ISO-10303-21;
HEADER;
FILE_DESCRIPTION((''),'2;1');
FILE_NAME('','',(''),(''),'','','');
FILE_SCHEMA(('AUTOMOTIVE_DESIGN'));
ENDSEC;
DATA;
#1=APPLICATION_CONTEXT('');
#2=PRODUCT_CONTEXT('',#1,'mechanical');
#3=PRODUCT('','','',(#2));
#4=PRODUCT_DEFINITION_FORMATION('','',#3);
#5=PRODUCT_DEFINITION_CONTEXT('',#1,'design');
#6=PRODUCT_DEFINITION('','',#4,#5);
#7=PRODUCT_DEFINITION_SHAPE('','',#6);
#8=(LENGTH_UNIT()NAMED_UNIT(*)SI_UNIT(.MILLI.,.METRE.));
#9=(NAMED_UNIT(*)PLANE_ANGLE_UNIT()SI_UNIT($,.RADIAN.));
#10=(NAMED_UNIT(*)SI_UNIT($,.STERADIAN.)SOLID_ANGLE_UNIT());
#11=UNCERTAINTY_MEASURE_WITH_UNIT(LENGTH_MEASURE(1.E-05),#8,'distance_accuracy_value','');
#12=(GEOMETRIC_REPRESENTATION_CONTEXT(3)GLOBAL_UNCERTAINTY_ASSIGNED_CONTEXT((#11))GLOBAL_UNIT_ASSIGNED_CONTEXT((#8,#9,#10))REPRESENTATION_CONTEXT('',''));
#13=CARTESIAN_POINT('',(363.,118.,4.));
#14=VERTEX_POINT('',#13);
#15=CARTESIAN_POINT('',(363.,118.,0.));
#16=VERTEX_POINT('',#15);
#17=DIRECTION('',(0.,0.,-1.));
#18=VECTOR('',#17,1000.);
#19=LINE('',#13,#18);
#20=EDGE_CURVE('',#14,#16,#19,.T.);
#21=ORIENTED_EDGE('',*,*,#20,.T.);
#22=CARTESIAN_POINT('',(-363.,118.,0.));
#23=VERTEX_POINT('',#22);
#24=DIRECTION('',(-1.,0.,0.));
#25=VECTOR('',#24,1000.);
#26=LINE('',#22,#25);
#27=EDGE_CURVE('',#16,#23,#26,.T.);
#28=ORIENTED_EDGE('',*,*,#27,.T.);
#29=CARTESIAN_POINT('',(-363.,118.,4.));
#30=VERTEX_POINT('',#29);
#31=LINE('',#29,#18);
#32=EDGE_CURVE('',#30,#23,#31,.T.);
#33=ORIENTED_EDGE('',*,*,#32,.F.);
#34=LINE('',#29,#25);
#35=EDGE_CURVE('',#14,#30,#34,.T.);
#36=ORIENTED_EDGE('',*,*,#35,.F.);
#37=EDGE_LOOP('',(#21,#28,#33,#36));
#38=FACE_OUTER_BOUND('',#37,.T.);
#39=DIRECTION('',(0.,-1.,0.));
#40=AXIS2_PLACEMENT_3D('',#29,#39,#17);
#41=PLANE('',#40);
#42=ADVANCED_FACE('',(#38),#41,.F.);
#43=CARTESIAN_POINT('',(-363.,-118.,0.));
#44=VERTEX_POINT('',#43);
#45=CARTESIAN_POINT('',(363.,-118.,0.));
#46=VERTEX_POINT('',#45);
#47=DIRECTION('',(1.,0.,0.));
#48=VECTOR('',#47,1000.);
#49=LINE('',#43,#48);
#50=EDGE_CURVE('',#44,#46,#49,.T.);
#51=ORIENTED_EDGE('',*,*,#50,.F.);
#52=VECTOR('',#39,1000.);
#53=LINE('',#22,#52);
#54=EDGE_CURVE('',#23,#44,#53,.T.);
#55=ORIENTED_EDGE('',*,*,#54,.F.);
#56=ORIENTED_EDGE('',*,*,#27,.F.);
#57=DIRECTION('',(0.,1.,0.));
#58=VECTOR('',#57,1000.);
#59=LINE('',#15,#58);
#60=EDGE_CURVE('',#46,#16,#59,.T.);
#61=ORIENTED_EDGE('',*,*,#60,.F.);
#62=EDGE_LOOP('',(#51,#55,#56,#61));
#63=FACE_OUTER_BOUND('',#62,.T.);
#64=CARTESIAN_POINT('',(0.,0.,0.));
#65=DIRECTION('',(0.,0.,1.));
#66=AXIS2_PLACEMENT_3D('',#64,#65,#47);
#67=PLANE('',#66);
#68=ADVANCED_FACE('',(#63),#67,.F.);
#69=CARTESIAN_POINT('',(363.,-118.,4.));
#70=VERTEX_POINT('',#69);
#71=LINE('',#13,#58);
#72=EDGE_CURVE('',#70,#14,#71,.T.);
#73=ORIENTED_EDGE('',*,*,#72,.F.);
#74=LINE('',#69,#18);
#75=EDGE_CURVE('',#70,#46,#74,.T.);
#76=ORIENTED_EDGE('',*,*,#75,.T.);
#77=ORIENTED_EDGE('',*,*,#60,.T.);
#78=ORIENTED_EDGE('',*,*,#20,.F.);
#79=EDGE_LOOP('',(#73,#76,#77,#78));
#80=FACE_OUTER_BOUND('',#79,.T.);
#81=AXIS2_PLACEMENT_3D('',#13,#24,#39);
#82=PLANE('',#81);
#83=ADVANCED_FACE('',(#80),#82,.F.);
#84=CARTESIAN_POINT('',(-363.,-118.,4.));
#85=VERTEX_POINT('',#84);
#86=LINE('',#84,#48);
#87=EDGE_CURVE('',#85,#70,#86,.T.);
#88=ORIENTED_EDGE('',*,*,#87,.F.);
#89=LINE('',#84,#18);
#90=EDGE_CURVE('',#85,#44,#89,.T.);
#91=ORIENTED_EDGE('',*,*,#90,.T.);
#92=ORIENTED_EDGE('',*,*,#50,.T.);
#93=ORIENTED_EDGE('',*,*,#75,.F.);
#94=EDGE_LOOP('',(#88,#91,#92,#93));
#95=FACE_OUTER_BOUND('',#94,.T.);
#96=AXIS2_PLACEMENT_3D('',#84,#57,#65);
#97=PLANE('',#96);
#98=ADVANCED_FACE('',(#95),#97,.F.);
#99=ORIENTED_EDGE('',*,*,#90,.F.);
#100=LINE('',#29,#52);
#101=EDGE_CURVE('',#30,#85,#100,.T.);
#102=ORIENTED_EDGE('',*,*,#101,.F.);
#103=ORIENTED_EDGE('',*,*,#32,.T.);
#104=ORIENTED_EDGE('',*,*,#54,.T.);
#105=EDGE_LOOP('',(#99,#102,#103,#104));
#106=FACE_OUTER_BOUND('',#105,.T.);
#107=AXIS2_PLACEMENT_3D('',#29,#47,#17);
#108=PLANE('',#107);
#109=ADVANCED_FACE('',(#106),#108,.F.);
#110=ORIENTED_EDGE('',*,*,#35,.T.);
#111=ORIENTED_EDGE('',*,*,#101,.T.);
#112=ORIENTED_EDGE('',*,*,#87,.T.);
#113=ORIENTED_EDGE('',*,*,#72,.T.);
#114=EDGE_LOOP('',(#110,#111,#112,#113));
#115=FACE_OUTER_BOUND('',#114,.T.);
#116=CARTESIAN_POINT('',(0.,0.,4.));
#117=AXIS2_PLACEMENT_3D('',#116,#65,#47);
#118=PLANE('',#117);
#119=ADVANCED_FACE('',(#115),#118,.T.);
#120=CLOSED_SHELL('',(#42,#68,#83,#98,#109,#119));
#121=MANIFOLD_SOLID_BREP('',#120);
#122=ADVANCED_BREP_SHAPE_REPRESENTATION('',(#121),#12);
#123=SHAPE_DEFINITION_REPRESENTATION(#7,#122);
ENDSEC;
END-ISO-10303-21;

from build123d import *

# Parameters (mm, degrees)
SKETCH_1_W      = 726
SKETCH_1_H      = 236
EXTRUDE_1_DEPTH = 4


with BuildPart() as part:
    # 草图1 → 凸台-拉伸1 (new body)
    with BuildSketch(Plane.XY):
        Rectangle(SKETCH_1_W, SKETCH_1_H)
    extrude(amount=EXTRUDE_1_DEPTH)


solid = part.part
